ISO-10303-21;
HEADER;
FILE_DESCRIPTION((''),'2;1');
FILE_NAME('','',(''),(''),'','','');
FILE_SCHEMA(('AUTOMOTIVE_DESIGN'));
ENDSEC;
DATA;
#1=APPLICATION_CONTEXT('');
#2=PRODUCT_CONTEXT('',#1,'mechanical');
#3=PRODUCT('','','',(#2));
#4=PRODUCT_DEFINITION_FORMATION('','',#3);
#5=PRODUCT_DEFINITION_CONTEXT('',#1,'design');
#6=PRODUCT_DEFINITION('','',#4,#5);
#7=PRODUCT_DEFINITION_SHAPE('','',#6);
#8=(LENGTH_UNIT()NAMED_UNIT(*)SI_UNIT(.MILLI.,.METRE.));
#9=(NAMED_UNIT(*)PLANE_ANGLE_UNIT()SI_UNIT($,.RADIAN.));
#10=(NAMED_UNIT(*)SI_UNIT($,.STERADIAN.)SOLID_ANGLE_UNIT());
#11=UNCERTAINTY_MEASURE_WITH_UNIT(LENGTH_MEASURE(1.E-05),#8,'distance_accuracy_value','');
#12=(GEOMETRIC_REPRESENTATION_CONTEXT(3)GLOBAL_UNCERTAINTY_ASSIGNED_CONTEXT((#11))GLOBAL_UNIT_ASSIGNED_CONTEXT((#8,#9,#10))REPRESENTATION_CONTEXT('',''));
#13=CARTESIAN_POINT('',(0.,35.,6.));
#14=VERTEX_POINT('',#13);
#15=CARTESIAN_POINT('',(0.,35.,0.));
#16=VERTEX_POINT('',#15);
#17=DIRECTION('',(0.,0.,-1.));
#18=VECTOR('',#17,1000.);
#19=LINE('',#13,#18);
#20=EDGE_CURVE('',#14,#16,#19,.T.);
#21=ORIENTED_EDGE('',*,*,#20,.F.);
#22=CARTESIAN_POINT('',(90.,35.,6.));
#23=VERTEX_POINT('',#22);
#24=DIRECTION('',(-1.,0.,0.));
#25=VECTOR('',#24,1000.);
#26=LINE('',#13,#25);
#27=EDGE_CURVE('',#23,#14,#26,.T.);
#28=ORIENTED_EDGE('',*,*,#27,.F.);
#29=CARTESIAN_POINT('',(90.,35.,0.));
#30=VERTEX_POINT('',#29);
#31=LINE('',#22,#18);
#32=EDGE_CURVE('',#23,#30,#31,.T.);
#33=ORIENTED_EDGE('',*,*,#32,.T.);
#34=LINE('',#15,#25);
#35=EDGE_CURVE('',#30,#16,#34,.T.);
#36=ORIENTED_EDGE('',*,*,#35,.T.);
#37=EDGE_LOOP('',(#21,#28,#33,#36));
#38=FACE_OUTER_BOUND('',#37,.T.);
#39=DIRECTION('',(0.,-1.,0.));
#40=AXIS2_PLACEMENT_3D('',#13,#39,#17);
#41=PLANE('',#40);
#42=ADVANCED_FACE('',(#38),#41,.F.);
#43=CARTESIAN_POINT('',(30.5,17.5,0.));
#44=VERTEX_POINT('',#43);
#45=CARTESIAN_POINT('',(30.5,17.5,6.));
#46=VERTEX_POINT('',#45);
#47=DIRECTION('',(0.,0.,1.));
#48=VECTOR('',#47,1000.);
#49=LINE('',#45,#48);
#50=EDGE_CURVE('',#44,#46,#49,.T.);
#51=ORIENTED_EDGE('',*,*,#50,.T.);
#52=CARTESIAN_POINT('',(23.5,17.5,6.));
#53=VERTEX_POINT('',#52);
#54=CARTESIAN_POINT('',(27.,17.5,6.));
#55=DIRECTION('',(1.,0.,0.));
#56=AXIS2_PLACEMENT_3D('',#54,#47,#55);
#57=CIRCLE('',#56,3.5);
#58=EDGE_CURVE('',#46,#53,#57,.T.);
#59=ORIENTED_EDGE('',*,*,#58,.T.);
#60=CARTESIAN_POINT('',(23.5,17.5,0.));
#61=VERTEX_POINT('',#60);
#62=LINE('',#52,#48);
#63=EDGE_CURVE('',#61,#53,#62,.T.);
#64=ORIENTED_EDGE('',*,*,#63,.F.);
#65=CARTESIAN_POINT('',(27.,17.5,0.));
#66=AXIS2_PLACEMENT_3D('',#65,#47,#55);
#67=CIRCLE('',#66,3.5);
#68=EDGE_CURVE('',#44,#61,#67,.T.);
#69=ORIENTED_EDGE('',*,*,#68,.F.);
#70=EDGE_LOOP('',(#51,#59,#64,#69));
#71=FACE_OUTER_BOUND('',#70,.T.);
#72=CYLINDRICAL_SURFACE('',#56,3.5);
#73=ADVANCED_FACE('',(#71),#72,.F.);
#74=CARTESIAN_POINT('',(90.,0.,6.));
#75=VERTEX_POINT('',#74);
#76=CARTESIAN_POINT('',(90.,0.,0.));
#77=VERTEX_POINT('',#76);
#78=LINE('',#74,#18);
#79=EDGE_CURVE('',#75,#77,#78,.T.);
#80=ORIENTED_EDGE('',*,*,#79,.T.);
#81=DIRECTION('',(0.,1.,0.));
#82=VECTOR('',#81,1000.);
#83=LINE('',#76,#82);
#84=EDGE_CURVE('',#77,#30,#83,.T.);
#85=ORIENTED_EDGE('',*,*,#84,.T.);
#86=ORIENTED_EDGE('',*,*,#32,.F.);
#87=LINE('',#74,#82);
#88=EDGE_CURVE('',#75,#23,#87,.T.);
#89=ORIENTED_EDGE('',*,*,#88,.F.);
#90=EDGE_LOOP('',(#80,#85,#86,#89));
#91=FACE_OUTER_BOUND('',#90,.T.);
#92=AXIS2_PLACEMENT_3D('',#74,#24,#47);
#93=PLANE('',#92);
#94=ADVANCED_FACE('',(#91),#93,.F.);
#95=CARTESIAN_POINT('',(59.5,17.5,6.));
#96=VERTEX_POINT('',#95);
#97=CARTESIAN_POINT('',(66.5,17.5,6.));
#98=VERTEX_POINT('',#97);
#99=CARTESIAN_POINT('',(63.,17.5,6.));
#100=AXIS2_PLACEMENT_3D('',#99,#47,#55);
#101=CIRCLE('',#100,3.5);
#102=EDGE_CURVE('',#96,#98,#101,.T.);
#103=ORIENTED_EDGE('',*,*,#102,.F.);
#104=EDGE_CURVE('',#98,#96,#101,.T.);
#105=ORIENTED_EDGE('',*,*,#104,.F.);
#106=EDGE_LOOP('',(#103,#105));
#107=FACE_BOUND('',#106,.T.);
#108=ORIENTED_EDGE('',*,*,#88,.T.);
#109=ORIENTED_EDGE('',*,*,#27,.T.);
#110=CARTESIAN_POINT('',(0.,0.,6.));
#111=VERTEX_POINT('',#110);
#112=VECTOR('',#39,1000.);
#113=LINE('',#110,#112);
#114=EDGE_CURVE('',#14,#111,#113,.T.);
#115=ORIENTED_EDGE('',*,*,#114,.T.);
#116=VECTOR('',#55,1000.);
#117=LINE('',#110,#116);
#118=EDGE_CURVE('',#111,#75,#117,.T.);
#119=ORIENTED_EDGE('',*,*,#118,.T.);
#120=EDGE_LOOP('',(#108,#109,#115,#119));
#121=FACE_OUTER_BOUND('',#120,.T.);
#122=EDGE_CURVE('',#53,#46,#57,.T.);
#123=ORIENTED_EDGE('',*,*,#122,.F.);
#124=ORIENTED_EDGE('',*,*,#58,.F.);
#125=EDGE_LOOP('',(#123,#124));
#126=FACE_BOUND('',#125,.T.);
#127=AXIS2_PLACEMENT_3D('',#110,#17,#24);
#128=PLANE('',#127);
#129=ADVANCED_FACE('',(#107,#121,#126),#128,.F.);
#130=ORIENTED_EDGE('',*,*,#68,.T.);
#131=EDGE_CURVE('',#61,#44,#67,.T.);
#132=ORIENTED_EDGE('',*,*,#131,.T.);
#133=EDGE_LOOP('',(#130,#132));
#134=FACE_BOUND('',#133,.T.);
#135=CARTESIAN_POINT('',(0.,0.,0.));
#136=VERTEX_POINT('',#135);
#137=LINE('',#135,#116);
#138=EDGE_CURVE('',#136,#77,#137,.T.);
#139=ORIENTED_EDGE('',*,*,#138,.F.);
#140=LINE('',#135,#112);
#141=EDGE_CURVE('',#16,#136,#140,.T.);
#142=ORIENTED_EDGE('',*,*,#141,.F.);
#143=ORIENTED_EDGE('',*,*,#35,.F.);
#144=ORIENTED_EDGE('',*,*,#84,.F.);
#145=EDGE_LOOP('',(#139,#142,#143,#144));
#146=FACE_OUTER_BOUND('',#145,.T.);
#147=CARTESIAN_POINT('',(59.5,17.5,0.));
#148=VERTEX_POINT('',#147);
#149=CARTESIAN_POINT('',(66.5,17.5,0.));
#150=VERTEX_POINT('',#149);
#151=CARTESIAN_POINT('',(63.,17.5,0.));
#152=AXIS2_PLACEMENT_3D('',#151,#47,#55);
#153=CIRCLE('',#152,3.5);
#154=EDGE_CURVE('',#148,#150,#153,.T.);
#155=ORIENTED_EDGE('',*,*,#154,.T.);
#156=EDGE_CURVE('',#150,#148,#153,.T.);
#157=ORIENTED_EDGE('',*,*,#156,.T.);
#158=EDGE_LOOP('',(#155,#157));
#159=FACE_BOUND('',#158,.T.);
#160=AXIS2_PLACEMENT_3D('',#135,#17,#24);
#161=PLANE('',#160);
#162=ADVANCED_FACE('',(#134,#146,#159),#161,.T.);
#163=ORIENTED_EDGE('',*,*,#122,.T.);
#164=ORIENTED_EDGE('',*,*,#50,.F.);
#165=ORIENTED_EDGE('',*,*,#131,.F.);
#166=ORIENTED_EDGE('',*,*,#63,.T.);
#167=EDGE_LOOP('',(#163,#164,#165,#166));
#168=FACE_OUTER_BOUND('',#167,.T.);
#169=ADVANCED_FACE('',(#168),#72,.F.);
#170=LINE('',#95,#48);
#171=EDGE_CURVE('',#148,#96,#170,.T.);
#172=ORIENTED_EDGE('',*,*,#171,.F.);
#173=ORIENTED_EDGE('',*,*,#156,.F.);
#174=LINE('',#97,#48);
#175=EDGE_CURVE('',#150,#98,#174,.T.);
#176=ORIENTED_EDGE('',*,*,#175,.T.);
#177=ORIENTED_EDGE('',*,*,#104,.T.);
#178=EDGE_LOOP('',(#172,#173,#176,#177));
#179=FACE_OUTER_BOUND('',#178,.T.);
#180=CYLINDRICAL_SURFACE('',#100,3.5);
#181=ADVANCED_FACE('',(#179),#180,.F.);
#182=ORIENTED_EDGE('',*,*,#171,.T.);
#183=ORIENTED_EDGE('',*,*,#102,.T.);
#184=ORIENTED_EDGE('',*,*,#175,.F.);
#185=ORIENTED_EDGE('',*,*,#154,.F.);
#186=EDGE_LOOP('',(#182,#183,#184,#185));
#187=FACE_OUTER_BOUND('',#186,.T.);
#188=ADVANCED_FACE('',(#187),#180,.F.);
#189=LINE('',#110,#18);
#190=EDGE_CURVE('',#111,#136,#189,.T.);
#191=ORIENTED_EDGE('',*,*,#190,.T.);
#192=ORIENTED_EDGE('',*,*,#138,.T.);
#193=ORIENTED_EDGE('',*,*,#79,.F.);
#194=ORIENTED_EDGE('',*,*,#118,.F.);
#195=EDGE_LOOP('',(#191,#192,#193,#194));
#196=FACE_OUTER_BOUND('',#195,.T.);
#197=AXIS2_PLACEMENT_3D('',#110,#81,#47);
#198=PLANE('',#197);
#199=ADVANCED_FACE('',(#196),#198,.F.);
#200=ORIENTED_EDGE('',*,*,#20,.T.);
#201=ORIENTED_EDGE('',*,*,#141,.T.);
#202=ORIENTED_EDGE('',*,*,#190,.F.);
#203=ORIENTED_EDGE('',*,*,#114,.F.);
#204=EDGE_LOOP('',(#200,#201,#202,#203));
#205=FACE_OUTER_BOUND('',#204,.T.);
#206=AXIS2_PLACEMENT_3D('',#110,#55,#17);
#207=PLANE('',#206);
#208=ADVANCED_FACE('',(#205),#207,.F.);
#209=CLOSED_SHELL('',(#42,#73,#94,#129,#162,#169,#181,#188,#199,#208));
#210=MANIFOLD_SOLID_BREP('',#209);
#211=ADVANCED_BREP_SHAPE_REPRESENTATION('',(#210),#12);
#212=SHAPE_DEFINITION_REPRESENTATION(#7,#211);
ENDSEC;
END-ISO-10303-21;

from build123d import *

# Parameters (mm, degrees)
SKETCH1_W            = 90
SKETCH1_H            = 35
BOSS_EXTRUDE1_DEPTH  = 6
M6_CLEARANCE_HOLE1_D = 7


with BuildPart() as part:
    # Sketch1 → Boss-Extrude1 (new body)
    with BuildSketch(Plane.XY):
        with Locations((45, 17.5)):
            Rectangle(SKETCH1_W, SKETCH1_H)
    extrude(amount=BOSS_EXTRUDE1_DEPTH)

    # M6 Clearance Hole1 (through all)
    with Locations(Plane.XY.offset(6)):
        with Locations((27, 17.5), (63, 17.5)):
            Hole(M6_CLEARANCE_HOLE1_D / 2)


solid = part.part
